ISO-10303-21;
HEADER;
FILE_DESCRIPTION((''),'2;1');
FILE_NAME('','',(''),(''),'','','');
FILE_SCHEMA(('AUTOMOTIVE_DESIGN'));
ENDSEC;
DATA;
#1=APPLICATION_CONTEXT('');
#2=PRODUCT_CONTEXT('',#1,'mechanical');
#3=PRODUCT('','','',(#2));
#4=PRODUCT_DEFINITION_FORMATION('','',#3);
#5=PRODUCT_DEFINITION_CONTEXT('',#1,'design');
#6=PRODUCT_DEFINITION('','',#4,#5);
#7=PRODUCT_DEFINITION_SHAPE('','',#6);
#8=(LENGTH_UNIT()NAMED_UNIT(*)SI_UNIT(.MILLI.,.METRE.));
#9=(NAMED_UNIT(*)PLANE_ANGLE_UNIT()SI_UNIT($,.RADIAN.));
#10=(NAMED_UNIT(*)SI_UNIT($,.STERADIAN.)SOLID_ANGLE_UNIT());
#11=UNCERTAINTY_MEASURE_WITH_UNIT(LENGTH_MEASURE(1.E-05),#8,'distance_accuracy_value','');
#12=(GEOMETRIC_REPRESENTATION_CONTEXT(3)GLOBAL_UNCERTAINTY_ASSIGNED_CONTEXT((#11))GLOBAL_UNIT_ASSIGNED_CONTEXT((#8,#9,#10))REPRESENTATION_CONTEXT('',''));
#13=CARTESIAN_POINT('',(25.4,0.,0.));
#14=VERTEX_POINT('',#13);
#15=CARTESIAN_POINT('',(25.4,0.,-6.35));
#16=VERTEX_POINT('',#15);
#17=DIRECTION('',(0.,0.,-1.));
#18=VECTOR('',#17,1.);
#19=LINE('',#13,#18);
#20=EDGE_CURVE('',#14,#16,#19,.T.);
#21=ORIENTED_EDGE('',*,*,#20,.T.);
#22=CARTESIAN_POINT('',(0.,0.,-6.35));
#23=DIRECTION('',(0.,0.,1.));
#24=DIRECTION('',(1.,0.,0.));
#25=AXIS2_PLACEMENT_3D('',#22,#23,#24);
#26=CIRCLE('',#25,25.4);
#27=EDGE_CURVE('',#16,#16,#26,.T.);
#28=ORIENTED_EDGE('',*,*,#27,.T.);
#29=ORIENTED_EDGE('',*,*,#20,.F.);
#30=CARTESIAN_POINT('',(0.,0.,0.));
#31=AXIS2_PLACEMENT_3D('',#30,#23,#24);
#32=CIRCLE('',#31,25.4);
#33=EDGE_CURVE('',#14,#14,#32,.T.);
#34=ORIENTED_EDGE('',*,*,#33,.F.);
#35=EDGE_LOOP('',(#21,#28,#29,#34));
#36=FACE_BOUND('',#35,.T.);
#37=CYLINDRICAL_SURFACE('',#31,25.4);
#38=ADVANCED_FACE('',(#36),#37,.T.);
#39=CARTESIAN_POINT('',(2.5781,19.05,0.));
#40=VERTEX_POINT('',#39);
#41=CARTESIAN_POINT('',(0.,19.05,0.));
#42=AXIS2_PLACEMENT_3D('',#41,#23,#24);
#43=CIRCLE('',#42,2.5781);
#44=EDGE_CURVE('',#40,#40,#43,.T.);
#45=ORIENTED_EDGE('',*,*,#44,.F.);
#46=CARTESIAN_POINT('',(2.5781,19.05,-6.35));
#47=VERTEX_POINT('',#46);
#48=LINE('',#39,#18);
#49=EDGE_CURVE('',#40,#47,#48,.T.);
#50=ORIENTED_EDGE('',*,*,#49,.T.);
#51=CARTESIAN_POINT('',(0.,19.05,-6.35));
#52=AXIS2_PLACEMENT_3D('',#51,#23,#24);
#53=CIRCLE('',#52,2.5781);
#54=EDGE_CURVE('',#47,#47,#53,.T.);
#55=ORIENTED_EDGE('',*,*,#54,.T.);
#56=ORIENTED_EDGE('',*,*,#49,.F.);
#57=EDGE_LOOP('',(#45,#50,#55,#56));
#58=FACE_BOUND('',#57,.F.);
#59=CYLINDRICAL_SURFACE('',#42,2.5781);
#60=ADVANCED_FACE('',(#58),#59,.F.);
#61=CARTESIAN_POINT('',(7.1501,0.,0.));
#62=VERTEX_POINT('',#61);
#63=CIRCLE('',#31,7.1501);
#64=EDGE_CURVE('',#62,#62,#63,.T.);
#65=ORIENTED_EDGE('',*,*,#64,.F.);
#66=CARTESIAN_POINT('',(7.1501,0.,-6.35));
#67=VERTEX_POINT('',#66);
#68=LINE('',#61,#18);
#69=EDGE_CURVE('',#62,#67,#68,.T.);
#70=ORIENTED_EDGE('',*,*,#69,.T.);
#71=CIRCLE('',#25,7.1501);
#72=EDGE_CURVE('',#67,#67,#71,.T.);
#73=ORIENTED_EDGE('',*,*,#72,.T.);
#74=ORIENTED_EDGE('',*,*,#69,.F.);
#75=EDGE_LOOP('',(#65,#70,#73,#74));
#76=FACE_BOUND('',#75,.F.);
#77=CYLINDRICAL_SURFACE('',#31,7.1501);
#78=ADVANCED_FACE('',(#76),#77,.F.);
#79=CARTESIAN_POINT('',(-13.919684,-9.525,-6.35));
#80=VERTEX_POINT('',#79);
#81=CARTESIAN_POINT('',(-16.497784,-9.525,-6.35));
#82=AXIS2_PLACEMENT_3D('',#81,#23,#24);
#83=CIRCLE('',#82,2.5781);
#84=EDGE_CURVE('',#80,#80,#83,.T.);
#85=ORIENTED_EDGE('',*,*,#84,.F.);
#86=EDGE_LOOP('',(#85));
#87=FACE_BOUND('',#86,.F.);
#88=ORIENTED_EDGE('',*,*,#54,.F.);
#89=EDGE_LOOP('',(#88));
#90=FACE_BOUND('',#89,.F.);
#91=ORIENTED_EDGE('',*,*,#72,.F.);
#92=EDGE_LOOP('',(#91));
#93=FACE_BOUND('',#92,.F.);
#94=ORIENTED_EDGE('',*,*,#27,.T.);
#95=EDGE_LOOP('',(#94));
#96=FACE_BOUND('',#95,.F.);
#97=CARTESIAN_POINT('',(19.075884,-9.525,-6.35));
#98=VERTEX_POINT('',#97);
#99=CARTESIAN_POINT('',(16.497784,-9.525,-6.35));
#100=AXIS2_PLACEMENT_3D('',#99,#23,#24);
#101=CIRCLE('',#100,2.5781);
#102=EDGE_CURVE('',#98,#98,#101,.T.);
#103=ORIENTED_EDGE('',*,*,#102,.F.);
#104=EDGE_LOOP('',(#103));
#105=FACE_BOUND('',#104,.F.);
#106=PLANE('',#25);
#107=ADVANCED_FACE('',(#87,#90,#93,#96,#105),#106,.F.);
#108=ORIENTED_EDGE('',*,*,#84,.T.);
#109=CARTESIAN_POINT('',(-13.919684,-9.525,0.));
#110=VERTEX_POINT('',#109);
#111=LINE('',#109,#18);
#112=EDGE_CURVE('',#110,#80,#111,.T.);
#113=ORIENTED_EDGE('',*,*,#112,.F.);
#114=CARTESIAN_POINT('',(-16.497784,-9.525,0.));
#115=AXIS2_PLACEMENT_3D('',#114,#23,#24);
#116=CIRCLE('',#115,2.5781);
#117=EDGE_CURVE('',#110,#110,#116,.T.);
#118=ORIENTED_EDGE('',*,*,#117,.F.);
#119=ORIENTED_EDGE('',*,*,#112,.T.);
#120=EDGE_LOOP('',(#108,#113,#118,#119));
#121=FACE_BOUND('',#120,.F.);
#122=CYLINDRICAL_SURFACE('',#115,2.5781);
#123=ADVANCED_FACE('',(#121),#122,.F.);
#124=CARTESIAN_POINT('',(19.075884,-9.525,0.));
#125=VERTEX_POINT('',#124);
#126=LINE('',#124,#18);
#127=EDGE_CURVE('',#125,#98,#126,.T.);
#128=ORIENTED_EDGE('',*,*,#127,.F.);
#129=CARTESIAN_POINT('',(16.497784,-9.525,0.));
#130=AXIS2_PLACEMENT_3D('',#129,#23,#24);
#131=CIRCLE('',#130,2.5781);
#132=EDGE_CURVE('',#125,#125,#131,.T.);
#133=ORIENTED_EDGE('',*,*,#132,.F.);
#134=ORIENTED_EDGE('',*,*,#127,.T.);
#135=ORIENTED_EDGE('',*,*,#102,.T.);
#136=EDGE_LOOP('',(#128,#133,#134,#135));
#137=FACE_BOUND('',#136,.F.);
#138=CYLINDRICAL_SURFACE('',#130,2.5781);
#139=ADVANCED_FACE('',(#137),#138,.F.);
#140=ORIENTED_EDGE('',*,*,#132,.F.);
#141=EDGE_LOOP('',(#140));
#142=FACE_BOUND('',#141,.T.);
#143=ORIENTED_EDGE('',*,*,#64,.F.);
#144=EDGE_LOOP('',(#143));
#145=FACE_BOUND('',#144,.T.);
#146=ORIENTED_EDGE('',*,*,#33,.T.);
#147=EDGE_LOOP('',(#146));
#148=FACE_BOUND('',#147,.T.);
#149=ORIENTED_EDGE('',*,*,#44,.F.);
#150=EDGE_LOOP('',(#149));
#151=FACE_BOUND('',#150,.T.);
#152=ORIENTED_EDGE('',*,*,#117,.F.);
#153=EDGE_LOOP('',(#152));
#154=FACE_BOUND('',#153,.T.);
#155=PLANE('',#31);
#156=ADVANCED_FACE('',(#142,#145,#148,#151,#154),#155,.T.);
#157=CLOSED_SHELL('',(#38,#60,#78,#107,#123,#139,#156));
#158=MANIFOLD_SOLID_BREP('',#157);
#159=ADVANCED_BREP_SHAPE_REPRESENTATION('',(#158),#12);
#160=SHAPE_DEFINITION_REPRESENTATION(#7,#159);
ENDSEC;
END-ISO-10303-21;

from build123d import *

# Parameters (mm, degrees)
SKETCH1_R           = 25.4
SKETCH1_R_2         = 7.1501
BOSS_EXTRUDE1_DEPTH = 6.35
SKETCH2_R           = 2.5781
CUT_EXTRUDE1_DEPTH  = 6.35


with BuildPart() as part:
    # Sketch1 → Boss-Extrude1 (new body)
    with BuildSketch(Plane.XY):
        Circle(SKETCH1_R)
        Circle(SKETCH1_R_2, mode=Mode.SUBTRACT)
    extrude(amount=-BOSS_EXTRUDE1_DEPTH)

    # Sketch2 → Cut-Extrude1 (cut)
    with BuildSketch(Plane.XY):
        with Locations((0, 19.05)):
            Circle(SKETCH2_R)
        with Locations((16.497783942, -9.525)):
            Circle(SKETCH2_R)
        with Locations((-16.497783942, -9.525)):
            Circle(SKETCH2_R)
    extrude(amount=-CUT_EXTRUDE1_DEPTH, mode=Mode.SUBTRACT)


solid = part.part
